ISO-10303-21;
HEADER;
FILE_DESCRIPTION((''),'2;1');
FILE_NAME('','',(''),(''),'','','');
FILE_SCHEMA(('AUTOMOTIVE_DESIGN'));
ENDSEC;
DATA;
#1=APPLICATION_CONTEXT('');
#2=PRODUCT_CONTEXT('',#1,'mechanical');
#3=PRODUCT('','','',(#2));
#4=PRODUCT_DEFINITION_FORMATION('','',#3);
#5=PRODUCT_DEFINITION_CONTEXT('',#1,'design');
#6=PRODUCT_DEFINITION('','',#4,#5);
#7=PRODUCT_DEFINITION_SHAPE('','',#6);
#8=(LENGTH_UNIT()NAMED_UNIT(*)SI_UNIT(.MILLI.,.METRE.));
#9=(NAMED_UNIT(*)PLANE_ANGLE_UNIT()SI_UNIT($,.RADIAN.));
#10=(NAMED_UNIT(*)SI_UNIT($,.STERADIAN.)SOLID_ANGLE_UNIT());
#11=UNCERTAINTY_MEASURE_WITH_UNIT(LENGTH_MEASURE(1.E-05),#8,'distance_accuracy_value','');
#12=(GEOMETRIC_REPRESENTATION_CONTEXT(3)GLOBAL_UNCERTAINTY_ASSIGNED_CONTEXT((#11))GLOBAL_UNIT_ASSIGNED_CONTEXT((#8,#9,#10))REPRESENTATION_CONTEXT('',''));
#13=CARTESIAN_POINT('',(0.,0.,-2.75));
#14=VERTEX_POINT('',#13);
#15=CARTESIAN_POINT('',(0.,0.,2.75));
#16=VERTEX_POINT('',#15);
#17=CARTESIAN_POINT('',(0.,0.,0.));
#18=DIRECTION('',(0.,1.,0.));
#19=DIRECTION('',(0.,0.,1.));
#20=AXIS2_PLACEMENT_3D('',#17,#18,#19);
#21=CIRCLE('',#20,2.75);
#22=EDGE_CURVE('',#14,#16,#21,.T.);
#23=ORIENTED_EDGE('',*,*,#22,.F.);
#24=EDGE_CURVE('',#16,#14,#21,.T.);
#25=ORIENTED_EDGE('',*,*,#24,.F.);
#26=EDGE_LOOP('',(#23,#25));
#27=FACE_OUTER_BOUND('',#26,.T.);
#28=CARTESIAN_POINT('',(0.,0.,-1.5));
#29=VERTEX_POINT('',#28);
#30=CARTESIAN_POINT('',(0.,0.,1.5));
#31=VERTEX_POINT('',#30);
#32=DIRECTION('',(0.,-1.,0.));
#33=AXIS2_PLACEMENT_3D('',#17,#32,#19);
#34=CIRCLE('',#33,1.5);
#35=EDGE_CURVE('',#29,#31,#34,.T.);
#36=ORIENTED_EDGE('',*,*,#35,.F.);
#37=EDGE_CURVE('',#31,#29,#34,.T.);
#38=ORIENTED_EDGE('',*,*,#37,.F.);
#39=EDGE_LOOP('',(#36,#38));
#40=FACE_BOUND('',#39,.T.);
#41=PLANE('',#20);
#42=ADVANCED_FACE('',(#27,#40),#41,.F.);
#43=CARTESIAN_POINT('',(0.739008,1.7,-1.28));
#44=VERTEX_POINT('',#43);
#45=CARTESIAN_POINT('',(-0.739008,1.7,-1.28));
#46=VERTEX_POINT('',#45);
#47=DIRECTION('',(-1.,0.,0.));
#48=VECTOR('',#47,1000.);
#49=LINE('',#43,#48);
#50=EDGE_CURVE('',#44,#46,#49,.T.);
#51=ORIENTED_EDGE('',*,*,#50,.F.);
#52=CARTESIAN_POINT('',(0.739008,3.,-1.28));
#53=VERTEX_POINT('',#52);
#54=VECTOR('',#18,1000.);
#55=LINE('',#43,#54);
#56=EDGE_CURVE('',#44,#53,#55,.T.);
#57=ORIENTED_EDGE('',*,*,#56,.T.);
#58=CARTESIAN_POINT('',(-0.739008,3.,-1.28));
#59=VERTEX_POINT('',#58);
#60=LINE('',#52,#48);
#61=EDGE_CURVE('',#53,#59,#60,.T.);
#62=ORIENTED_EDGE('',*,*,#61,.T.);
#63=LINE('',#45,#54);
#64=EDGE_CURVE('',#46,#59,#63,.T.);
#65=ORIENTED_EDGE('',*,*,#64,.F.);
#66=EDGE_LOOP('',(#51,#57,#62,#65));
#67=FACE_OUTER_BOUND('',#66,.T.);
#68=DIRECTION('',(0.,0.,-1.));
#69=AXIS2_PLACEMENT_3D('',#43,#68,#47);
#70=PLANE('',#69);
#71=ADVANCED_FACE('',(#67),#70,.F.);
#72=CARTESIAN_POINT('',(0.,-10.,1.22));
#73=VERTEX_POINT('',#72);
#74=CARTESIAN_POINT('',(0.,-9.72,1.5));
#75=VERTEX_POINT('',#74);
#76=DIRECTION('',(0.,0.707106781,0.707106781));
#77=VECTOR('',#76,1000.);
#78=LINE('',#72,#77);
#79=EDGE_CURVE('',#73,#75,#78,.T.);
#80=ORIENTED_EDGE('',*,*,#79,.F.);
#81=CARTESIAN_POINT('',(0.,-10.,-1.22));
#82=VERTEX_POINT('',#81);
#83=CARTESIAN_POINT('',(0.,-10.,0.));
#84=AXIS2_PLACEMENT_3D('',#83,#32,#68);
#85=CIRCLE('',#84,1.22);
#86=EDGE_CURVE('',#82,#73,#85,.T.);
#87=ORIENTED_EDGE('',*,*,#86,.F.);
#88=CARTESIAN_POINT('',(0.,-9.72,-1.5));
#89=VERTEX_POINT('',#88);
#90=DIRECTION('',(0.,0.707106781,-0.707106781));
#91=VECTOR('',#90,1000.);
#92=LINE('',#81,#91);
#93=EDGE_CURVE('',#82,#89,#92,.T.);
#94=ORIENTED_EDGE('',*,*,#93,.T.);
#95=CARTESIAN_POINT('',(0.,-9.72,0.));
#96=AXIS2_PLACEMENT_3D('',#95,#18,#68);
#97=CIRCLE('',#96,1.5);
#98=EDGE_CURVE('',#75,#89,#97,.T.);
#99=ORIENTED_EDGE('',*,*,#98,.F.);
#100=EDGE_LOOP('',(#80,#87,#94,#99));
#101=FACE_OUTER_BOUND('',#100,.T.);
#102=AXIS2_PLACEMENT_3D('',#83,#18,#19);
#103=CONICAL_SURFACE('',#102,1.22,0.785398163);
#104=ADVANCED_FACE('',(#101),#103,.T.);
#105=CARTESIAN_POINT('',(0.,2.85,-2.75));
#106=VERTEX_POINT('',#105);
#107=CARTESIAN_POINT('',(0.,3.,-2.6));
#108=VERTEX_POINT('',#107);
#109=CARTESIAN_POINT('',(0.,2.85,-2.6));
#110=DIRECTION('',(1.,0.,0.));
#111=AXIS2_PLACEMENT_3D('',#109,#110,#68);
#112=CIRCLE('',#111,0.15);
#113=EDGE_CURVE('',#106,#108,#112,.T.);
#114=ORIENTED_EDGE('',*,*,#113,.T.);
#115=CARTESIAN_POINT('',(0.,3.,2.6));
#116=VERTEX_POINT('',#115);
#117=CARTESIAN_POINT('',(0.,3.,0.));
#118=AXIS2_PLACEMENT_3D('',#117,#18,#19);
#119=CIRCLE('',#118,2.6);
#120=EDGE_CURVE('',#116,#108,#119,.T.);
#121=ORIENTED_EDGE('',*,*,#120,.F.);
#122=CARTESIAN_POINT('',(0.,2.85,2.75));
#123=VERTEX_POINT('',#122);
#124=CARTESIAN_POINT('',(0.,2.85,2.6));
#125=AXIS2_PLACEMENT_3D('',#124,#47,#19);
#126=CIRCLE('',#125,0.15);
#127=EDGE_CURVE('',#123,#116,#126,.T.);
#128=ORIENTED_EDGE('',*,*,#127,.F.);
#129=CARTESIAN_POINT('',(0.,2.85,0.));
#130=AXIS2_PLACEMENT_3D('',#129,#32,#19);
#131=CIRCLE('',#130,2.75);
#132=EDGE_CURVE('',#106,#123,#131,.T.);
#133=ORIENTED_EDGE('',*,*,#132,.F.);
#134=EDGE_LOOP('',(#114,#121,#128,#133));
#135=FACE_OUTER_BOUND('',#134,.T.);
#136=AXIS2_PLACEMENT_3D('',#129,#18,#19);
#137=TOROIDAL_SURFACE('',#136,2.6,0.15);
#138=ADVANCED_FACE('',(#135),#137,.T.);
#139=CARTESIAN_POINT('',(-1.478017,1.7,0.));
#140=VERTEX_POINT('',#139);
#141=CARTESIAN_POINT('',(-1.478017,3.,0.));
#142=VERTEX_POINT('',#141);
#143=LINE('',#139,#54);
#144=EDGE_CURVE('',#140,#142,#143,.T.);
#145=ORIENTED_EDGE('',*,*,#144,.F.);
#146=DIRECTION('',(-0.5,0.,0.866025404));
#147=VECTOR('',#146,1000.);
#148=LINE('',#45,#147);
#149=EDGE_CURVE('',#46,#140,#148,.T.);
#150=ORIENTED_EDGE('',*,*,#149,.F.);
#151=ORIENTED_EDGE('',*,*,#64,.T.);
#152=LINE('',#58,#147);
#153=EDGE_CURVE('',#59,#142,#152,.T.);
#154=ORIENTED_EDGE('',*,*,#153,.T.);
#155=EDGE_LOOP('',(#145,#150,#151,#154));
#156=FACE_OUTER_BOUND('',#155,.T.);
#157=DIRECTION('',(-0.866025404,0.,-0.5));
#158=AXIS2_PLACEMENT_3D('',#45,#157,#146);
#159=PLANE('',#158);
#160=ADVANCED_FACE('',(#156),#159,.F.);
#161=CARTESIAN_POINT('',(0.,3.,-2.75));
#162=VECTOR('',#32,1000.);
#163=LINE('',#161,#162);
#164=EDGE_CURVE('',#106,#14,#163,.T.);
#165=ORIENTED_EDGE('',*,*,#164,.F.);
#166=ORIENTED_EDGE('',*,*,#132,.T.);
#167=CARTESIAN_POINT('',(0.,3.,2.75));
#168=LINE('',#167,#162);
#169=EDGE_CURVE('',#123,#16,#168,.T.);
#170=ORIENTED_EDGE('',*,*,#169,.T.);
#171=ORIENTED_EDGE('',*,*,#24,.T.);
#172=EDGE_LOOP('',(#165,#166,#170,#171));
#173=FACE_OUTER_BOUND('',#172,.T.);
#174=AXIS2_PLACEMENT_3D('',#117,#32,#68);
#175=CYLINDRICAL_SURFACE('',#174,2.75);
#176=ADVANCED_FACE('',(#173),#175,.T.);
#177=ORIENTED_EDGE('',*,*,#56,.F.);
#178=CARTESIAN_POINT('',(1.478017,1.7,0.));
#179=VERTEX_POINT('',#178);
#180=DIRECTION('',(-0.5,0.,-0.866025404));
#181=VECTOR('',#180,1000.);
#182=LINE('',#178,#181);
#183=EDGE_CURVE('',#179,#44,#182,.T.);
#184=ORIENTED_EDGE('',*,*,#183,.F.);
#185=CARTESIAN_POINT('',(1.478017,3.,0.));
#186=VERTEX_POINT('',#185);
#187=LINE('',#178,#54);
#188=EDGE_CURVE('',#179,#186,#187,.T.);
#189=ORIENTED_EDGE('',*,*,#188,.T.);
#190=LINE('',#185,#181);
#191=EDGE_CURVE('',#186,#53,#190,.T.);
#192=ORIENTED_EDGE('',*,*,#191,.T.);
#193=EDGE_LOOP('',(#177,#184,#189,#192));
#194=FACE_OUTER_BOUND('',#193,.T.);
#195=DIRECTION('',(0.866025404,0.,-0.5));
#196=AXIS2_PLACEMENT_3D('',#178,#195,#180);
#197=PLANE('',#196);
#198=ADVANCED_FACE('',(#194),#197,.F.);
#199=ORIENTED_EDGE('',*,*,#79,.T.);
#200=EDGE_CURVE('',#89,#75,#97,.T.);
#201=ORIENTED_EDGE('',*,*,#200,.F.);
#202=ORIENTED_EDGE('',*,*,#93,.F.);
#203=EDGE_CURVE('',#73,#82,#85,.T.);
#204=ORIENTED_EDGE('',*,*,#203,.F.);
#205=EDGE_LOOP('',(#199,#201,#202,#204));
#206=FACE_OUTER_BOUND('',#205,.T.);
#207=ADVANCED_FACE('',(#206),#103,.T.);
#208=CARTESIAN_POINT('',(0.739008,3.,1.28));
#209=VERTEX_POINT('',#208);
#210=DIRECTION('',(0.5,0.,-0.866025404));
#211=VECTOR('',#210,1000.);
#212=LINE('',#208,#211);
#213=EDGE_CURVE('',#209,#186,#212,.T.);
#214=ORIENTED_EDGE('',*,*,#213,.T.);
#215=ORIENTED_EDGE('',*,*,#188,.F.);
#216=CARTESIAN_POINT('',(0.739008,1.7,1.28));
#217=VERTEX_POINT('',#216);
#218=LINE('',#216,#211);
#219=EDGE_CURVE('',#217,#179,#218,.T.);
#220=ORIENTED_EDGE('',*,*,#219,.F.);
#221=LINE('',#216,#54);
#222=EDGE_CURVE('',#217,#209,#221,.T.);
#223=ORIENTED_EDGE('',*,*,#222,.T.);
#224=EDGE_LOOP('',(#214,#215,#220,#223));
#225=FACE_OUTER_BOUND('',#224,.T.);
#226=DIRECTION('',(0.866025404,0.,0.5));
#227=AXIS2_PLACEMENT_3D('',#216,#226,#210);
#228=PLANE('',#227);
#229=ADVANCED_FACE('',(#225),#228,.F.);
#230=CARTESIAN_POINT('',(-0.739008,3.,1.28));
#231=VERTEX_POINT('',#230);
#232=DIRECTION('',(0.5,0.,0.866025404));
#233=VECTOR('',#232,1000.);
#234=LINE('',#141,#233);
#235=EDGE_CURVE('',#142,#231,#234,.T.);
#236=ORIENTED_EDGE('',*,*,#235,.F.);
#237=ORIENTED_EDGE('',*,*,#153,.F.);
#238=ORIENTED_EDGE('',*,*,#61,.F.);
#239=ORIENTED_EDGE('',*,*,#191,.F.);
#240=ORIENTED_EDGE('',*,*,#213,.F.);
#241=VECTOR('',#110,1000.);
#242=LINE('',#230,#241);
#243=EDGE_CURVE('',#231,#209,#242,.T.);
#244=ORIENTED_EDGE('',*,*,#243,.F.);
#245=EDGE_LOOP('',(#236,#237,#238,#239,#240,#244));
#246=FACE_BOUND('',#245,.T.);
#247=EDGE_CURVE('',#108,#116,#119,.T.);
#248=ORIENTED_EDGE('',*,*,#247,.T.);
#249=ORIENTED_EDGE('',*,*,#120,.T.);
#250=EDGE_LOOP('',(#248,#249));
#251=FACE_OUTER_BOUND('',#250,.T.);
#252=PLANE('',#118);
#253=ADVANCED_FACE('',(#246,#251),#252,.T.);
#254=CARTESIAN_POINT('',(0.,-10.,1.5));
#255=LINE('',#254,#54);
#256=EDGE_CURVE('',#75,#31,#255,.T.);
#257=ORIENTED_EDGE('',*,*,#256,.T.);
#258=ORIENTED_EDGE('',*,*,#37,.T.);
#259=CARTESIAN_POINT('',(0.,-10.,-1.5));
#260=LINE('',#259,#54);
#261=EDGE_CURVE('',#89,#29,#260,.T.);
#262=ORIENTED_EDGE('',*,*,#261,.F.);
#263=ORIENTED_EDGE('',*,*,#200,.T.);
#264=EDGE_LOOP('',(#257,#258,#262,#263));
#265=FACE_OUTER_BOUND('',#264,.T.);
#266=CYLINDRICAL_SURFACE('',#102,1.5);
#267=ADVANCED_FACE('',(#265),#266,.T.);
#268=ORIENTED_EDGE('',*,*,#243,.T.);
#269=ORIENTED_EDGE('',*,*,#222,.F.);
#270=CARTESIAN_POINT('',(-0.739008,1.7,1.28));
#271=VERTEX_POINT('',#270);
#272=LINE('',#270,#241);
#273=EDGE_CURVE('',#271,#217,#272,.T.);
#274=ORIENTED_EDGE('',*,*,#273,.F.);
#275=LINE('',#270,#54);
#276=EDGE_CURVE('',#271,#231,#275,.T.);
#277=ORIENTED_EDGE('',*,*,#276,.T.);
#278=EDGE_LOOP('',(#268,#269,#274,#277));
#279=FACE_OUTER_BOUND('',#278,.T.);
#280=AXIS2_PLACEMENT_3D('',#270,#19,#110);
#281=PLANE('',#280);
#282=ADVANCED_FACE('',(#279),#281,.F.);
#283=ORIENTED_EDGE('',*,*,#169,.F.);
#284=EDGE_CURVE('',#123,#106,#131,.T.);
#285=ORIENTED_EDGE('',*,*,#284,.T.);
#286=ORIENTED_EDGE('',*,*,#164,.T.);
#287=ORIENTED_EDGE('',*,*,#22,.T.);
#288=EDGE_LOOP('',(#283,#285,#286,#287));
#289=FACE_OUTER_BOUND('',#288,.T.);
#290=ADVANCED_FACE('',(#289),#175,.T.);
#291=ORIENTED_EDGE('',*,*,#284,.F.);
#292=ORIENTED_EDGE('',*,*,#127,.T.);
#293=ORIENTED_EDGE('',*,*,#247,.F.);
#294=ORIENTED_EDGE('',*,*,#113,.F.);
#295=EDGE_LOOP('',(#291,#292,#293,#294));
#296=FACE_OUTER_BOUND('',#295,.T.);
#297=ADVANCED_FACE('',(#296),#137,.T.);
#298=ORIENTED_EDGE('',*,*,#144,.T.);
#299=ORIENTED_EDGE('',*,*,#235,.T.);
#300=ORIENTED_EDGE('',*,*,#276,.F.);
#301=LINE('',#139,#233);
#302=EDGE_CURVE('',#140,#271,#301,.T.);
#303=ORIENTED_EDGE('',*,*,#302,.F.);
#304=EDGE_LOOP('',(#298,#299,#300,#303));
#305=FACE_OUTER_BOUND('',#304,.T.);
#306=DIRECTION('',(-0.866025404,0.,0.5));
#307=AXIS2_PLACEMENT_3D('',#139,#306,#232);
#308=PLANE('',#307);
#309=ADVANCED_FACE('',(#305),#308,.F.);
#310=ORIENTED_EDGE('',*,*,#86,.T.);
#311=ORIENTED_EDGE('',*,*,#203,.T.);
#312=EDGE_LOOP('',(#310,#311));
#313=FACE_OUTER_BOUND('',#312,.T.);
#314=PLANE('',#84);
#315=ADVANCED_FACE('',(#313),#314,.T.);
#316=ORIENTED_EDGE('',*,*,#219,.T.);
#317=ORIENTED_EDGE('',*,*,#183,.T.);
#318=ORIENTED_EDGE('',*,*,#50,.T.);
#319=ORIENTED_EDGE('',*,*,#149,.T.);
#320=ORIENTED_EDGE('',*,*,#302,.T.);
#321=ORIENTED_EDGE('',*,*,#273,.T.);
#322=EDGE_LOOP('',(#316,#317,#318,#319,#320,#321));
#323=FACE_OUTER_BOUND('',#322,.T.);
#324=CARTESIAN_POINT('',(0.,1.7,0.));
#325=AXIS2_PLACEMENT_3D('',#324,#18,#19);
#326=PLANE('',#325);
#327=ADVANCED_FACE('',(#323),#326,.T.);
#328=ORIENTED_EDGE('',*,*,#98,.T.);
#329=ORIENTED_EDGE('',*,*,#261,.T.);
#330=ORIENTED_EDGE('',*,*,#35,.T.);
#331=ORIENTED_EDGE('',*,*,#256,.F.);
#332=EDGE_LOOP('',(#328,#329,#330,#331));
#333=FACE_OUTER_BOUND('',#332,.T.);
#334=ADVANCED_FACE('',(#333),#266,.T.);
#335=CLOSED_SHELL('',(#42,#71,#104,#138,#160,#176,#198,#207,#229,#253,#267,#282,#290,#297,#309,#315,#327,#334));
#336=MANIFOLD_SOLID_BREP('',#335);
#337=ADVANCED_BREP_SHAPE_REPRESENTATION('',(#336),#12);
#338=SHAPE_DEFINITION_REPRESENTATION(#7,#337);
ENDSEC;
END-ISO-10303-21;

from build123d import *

# Parameters (mm, degrees)
SKETCH_1_R          = 2.75
EXTRUDE_1_DEPTH     = 3
CUT_EXTRUDE_1_DEPTH = 1.3
FILLET_1_R          = 0.15
SKETCH_5_R          = 1.5
EXTRUDE_2_DEPTH     = 10
CHAMFER_2_SIZE      = 0.28


with BuildPart() as part:
    # 草图1 → 凸台-拉伸1 (new body)
    with BuildSketch(Plane(origin=(0, 0, 0), x_dir=(1, 0, 0), z_dir=(0, 1, 0))):
        with Locations(Location((0, 0, 0), (0, 0, 270))):
            Circle(SKETCH_1_R)
    extrude(amount=EXTRUDE_1_DEPTH)

    # 草图2 → 切除-拉伸1 (cut)
    with BuildSketch(Plane(origin=(0, 3, 0), x_dir=(1, 0, 0), z_dir=(0, 1, 0))):
        Polygon((1.478016689, 0), (0.739008345, 1.28), (-0.739008345, 1.28), (-1.478016689, 0), (-0.739008345, -1.28), (0.739008345, -1.28), align=None)
    extrude(amount=-CUT_EXTRUDE_1_DEPTH, mode=Mode.SUBTRACT)

    # 圆角1
    fillet_1_edges = [part.edges().sort_by_distance(p)[0] for p in [
        (0, 3, -2.75),
    ]]
    fillet(fillet_1_edges, radius=FILLET_1_R)

    # 草图5 → 凸台-拉伸2 (add)
    with BuildSketch(Plane.XZ):
        with Locations(Location((0, 0, 0), (0, 0, 90))):
            Circle(SKETCH_5_R)
    extrude(amount=EXTRUDE_2_DEPTH)

    # 倒角2
    chamfer_2_edges = [part.edges().sort_by_distance(p)[0] for p in [
        (0, -10, -1.5),
    ]]
    chamfer(chamfer_2_edges, length=CHAMFER_2_SIZE)


solid = part.part
